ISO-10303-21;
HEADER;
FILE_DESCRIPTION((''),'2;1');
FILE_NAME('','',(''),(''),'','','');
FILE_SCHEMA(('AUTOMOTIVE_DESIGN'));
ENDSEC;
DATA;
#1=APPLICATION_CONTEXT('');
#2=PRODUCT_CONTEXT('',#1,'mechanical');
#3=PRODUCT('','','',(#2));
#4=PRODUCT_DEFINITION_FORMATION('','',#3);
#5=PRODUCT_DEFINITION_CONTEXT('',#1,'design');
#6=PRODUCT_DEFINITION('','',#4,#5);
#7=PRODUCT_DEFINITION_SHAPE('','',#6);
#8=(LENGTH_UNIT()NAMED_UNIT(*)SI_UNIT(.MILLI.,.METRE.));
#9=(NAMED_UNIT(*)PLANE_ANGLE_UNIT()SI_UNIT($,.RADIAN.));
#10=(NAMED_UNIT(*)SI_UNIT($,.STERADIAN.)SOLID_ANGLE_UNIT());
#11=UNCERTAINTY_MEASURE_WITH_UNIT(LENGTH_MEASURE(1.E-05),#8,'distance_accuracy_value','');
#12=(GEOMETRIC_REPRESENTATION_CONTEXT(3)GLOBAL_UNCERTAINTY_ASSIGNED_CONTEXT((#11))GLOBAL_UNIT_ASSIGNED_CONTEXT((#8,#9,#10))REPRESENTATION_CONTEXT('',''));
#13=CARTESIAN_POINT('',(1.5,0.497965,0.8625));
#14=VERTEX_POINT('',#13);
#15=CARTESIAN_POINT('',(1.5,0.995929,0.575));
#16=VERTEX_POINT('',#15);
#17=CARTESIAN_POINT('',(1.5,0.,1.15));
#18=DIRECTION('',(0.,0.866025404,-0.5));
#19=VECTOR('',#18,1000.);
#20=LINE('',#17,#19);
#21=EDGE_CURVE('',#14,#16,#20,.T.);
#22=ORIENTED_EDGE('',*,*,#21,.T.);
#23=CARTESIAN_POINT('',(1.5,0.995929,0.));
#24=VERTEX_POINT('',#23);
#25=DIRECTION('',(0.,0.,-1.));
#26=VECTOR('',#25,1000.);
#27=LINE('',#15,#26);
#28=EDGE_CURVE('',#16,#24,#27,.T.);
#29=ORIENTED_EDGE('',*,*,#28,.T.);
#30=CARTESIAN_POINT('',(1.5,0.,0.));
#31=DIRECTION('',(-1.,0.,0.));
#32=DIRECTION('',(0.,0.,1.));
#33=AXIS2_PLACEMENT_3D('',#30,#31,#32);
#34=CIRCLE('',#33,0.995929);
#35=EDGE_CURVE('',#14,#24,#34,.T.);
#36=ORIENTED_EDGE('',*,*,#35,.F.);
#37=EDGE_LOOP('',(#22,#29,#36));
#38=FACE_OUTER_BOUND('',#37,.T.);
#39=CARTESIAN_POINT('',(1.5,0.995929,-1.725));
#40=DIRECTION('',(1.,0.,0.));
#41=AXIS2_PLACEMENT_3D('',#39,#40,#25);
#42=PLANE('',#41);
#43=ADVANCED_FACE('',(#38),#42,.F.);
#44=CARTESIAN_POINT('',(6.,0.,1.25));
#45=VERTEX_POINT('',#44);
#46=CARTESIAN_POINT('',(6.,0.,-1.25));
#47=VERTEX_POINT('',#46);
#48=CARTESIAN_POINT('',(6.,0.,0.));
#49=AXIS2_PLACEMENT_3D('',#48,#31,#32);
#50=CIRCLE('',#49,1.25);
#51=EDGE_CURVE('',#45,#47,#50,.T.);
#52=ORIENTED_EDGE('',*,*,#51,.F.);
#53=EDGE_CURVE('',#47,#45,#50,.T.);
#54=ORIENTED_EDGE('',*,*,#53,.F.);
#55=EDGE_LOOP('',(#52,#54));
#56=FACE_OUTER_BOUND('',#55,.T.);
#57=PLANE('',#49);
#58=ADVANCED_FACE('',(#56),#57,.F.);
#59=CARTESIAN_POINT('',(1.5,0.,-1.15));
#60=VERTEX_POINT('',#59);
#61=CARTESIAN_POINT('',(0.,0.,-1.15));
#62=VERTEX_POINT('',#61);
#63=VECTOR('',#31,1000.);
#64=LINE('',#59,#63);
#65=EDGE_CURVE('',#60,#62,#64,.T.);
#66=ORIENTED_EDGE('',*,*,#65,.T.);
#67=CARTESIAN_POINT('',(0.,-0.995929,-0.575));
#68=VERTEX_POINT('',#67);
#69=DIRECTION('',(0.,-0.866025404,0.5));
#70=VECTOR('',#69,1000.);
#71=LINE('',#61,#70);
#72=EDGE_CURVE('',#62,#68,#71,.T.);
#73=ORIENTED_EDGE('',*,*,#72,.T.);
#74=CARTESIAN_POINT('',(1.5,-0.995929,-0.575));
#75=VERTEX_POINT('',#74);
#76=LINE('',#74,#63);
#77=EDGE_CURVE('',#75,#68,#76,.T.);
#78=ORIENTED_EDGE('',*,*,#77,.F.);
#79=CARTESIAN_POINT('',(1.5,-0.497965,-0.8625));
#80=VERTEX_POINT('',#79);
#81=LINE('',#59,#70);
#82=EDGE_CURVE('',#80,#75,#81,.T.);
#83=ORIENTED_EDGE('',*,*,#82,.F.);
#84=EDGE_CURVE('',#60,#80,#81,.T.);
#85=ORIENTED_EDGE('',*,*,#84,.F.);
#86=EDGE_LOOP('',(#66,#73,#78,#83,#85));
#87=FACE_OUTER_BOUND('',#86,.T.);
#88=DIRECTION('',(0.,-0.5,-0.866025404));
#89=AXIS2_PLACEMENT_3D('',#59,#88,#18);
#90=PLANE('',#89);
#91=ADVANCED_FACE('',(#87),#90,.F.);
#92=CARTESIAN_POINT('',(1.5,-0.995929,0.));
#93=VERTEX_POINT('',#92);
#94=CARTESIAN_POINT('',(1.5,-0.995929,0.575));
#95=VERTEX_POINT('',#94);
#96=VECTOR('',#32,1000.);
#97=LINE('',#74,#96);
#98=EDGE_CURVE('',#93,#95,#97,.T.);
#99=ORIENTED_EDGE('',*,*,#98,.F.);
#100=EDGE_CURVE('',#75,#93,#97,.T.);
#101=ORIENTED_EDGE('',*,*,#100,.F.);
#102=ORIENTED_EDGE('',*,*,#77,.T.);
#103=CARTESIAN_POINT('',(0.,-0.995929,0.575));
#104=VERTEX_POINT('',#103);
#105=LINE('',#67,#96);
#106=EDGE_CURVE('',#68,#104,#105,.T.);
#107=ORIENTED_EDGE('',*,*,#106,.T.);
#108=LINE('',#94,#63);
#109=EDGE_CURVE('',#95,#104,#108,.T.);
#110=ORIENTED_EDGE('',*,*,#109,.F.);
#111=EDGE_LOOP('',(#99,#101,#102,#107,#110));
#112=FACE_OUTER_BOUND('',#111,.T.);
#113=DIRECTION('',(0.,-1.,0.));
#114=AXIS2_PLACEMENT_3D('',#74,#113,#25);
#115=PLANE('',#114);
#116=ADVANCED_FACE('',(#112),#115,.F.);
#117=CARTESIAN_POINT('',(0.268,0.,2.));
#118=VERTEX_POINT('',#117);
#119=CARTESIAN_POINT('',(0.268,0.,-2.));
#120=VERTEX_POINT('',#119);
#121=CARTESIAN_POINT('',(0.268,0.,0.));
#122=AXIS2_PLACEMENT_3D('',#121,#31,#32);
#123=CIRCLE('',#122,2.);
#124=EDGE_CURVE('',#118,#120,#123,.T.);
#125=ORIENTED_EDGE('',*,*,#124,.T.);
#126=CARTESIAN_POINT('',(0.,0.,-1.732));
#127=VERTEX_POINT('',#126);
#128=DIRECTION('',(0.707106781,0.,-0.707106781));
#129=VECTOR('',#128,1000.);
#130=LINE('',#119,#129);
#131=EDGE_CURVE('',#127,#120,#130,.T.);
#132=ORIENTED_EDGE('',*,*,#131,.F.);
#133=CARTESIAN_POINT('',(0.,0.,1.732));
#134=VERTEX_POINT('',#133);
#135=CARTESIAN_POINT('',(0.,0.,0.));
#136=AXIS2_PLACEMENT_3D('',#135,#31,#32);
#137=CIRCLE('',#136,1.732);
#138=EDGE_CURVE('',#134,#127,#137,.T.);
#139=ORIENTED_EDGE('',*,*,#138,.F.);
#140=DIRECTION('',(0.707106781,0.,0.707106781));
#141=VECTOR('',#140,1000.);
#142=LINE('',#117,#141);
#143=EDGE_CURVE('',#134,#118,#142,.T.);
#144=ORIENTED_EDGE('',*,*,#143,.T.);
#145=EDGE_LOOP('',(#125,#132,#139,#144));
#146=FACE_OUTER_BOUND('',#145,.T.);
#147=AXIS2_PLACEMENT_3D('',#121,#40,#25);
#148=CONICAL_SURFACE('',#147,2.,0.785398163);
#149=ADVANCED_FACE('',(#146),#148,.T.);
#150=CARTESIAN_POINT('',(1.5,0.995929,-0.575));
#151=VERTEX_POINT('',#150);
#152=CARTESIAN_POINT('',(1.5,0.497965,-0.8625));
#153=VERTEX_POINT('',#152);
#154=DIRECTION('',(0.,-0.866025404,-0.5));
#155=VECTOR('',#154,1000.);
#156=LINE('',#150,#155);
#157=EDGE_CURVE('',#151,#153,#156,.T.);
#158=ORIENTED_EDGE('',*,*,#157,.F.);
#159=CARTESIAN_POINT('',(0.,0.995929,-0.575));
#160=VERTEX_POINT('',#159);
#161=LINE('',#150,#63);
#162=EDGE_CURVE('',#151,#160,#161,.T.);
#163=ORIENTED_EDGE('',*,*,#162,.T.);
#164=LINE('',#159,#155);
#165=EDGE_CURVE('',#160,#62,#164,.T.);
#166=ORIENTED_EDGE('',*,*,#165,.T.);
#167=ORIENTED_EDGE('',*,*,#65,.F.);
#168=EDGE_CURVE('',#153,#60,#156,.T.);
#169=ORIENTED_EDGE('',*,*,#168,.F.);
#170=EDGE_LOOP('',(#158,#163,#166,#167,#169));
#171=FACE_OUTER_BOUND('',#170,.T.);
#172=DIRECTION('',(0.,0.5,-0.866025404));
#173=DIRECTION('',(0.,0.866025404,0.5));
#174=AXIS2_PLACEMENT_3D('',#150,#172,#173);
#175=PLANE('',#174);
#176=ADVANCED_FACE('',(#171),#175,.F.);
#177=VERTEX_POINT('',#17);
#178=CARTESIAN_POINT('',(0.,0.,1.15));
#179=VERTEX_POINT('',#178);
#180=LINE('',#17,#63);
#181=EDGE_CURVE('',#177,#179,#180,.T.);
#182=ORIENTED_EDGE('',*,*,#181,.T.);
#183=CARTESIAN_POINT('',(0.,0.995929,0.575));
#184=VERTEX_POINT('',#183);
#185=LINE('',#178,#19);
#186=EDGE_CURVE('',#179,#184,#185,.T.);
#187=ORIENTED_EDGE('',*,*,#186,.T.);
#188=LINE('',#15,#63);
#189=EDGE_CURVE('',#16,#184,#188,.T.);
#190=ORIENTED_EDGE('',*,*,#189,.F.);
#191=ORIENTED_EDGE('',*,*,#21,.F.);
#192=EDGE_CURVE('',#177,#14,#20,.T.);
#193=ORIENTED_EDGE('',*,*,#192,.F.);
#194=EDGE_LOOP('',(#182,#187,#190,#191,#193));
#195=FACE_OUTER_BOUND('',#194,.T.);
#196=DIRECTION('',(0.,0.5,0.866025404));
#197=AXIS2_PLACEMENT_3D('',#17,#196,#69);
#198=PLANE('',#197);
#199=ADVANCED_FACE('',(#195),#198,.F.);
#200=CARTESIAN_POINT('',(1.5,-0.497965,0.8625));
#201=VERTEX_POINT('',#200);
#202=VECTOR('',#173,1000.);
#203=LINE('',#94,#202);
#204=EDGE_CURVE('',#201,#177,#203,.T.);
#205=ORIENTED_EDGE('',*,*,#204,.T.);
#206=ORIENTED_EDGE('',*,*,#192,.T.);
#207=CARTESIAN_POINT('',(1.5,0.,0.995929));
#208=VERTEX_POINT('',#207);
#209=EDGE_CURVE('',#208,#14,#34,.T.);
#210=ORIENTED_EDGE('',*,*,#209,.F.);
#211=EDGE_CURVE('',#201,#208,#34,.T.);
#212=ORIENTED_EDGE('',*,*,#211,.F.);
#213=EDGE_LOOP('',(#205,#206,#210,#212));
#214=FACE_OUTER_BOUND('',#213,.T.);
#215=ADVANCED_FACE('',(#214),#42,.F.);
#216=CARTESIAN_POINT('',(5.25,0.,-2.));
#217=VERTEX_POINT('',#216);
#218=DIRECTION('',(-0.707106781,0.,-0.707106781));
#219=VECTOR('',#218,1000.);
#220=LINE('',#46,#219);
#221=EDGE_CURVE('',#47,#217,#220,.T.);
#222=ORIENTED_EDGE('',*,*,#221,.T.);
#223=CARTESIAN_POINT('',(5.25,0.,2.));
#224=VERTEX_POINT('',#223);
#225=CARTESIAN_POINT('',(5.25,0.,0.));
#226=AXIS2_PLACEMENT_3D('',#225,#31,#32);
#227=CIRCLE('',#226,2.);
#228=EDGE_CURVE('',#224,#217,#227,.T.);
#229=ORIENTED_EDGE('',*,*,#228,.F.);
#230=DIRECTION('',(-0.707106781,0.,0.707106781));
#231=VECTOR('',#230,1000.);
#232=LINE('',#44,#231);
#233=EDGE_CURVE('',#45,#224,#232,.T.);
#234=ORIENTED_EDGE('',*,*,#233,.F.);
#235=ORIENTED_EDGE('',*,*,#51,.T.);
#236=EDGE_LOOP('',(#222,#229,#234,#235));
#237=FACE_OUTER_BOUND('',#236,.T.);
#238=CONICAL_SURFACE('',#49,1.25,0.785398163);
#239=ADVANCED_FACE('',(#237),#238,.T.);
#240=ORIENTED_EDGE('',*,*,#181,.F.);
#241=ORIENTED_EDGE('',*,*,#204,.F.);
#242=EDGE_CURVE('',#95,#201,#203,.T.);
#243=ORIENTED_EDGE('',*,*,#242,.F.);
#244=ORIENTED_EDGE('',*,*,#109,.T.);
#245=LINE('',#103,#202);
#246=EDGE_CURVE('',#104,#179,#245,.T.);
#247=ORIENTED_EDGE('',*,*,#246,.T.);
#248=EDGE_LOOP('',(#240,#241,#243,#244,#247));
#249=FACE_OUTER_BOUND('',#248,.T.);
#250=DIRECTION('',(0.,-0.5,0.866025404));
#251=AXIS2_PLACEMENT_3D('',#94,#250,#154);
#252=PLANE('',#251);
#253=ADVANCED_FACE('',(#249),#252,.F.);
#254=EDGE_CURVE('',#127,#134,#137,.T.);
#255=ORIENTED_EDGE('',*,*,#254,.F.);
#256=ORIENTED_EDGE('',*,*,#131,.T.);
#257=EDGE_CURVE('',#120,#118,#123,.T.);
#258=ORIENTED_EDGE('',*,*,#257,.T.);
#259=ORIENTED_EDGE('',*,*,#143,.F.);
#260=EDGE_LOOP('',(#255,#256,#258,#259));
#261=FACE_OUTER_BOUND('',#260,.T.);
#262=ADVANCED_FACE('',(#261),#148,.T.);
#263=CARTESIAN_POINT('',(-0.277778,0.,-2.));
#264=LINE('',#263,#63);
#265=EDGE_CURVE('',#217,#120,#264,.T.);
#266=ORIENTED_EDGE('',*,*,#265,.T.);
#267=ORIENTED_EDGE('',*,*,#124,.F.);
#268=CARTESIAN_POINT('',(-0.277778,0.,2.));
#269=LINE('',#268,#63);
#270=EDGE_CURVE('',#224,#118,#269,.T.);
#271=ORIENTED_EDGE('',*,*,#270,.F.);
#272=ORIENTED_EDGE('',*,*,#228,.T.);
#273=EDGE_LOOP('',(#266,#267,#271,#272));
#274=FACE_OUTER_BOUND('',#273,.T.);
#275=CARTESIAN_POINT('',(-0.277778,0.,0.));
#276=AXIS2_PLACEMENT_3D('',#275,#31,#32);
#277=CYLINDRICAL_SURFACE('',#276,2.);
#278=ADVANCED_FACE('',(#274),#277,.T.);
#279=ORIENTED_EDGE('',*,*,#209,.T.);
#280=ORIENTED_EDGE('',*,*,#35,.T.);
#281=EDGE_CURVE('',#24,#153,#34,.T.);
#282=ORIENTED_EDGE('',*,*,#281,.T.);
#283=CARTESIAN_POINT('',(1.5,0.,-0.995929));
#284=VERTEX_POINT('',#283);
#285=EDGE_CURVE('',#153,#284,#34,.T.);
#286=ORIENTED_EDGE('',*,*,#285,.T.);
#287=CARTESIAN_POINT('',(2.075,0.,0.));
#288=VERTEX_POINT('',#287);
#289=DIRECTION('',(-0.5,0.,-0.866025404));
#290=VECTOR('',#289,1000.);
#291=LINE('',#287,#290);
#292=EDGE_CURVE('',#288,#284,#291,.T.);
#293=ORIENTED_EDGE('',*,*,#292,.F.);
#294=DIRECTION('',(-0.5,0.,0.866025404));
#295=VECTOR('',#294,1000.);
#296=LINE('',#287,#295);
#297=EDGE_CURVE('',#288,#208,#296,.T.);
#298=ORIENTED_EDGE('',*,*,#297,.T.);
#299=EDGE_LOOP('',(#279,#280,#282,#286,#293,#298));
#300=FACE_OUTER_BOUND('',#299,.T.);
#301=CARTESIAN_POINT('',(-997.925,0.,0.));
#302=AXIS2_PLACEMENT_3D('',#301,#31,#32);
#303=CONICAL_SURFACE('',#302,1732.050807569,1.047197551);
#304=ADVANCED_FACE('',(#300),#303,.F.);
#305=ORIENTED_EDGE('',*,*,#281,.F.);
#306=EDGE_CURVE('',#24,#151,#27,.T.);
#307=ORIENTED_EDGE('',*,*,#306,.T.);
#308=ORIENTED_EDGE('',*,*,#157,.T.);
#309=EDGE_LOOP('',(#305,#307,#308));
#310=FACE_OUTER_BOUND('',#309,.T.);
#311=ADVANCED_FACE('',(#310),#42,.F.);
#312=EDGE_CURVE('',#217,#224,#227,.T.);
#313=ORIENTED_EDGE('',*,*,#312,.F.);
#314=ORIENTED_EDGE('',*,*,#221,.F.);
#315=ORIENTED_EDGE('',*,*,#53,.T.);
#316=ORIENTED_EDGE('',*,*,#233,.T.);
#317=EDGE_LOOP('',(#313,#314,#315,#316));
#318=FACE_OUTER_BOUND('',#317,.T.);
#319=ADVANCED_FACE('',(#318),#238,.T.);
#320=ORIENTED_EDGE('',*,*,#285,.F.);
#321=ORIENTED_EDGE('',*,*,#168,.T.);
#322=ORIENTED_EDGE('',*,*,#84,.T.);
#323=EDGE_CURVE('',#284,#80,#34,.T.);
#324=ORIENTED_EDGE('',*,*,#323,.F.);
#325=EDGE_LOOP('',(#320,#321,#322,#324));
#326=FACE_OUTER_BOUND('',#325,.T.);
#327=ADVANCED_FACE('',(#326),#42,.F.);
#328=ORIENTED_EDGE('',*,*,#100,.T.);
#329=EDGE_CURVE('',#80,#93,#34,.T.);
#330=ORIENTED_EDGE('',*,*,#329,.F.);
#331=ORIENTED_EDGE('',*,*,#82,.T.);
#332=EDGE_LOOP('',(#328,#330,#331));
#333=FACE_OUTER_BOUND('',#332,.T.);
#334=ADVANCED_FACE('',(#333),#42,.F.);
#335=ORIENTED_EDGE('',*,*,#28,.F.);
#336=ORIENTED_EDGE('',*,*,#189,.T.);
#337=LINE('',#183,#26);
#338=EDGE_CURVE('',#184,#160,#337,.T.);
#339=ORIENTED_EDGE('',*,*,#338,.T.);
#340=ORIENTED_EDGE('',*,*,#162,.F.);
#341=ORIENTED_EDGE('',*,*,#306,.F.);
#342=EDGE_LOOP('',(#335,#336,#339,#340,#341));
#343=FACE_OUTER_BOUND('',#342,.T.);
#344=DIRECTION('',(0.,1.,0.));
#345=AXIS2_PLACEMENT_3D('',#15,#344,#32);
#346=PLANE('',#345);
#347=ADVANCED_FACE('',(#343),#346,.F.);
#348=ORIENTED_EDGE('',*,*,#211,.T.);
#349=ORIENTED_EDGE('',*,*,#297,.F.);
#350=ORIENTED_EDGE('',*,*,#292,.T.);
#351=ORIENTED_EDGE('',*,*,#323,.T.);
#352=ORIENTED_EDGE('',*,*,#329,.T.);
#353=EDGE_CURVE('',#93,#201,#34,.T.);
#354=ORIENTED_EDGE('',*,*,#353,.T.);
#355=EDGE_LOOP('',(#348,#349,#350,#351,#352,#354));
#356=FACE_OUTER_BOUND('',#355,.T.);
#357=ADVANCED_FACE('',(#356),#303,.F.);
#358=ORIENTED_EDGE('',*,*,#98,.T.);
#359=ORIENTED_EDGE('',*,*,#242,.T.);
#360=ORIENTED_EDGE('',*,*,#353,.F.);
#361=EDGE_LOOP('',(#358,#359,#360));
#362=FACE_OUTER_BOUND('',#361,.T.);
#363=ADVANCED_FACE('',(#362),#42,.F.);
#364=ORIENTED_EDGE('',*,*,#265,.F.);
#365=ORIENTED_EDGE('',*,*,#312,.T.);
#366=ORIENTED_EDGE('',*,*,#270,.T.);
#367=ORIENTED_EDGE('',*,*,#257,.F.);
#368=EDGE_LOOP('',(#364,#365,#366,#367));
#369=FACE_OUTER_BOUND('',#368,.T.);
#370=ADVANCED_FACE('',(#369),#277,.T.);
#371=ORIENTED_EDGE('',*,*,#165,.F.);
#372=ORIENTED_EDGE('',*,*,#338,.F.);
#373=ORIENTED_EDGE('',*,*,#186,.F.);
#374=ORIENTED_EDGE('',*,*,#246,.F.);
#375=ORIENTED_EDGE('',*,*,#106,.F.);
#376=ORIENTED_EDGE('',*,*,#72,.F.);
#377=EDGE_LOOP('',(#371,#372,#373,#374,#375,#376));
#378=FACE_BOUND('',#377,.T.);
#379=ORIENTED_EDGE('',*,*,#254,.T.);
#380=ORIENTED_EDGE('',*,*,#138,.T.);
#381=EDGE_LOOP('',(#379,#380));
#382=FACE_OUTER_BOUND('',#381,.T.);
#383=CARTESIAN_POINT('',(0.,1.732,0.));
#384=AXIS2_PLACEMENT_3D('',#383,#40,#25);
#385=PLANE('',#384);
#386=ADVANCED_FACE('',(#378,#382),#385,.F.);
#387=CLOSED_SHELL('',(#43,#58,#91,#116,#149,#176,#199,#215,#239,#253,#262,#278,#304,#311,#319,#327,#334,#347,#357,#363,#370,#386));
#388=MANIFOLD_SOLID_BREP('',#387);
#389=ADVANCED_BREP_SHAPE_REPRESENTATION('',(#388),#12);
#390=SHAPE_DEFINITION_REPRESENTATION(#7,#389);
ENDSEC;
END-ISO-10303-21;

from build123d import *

# Parameters (mm, degrees)
CUT_EXTRUDE1_DEPTH = 1.5


with BuildPart() as part:
    # Sketch1 → Boss-Revolve (revolve)
    with BuildSketch(Plane.XY, mode=Mode.PRIVATE) as boss_revolve_sk:
        Polygon((0, 0), (6, 0), (6, 1.25), (5.25, 2), (0.268, 2), (0, 1.732), align=None)
    revolve(boss_revolve_sk.sketch.rotate(Axis((-0.277777778, 0, 0), (1, 0, 0)), 90), axis=Axis((-0.277777778, 0, 0), (1, 0, 0)))

    # Sketch2 → Cut-Extrude1 (cut)
    with BuildSketch(Plane.ZY):
        Polygon((-0.575, -0.995929214), (0.575, -0.995929214), (1.15, 0), (0.575, 0.995929214), (-0.575, 0.995929214), (-1.15, 0), align=None)
    extrude(amount=-CUT_EXTRUDE1_DEPTH, mode=Mode.SUBTRACT)

    # Sketch4 → Cut-Revolve2 (revolve, cut)
    with BuildSketch(Plane.XY, mode=Mode.PRIVATE) as cut_revolve2_sk:
        Polygon((1.5, 0.995929214), (2.075, 0), (1.5, 0), align=None)
    revolve(cut_revolve2_sk.sketch.rotate(Axis((-0.277777778, 0, 0), (1, 0, 0)), 90), axis=Axis((-0.277777778, 0, 0), (1, 0, 0)), mode=Mode.SUBTRACT)


solid = part.part
